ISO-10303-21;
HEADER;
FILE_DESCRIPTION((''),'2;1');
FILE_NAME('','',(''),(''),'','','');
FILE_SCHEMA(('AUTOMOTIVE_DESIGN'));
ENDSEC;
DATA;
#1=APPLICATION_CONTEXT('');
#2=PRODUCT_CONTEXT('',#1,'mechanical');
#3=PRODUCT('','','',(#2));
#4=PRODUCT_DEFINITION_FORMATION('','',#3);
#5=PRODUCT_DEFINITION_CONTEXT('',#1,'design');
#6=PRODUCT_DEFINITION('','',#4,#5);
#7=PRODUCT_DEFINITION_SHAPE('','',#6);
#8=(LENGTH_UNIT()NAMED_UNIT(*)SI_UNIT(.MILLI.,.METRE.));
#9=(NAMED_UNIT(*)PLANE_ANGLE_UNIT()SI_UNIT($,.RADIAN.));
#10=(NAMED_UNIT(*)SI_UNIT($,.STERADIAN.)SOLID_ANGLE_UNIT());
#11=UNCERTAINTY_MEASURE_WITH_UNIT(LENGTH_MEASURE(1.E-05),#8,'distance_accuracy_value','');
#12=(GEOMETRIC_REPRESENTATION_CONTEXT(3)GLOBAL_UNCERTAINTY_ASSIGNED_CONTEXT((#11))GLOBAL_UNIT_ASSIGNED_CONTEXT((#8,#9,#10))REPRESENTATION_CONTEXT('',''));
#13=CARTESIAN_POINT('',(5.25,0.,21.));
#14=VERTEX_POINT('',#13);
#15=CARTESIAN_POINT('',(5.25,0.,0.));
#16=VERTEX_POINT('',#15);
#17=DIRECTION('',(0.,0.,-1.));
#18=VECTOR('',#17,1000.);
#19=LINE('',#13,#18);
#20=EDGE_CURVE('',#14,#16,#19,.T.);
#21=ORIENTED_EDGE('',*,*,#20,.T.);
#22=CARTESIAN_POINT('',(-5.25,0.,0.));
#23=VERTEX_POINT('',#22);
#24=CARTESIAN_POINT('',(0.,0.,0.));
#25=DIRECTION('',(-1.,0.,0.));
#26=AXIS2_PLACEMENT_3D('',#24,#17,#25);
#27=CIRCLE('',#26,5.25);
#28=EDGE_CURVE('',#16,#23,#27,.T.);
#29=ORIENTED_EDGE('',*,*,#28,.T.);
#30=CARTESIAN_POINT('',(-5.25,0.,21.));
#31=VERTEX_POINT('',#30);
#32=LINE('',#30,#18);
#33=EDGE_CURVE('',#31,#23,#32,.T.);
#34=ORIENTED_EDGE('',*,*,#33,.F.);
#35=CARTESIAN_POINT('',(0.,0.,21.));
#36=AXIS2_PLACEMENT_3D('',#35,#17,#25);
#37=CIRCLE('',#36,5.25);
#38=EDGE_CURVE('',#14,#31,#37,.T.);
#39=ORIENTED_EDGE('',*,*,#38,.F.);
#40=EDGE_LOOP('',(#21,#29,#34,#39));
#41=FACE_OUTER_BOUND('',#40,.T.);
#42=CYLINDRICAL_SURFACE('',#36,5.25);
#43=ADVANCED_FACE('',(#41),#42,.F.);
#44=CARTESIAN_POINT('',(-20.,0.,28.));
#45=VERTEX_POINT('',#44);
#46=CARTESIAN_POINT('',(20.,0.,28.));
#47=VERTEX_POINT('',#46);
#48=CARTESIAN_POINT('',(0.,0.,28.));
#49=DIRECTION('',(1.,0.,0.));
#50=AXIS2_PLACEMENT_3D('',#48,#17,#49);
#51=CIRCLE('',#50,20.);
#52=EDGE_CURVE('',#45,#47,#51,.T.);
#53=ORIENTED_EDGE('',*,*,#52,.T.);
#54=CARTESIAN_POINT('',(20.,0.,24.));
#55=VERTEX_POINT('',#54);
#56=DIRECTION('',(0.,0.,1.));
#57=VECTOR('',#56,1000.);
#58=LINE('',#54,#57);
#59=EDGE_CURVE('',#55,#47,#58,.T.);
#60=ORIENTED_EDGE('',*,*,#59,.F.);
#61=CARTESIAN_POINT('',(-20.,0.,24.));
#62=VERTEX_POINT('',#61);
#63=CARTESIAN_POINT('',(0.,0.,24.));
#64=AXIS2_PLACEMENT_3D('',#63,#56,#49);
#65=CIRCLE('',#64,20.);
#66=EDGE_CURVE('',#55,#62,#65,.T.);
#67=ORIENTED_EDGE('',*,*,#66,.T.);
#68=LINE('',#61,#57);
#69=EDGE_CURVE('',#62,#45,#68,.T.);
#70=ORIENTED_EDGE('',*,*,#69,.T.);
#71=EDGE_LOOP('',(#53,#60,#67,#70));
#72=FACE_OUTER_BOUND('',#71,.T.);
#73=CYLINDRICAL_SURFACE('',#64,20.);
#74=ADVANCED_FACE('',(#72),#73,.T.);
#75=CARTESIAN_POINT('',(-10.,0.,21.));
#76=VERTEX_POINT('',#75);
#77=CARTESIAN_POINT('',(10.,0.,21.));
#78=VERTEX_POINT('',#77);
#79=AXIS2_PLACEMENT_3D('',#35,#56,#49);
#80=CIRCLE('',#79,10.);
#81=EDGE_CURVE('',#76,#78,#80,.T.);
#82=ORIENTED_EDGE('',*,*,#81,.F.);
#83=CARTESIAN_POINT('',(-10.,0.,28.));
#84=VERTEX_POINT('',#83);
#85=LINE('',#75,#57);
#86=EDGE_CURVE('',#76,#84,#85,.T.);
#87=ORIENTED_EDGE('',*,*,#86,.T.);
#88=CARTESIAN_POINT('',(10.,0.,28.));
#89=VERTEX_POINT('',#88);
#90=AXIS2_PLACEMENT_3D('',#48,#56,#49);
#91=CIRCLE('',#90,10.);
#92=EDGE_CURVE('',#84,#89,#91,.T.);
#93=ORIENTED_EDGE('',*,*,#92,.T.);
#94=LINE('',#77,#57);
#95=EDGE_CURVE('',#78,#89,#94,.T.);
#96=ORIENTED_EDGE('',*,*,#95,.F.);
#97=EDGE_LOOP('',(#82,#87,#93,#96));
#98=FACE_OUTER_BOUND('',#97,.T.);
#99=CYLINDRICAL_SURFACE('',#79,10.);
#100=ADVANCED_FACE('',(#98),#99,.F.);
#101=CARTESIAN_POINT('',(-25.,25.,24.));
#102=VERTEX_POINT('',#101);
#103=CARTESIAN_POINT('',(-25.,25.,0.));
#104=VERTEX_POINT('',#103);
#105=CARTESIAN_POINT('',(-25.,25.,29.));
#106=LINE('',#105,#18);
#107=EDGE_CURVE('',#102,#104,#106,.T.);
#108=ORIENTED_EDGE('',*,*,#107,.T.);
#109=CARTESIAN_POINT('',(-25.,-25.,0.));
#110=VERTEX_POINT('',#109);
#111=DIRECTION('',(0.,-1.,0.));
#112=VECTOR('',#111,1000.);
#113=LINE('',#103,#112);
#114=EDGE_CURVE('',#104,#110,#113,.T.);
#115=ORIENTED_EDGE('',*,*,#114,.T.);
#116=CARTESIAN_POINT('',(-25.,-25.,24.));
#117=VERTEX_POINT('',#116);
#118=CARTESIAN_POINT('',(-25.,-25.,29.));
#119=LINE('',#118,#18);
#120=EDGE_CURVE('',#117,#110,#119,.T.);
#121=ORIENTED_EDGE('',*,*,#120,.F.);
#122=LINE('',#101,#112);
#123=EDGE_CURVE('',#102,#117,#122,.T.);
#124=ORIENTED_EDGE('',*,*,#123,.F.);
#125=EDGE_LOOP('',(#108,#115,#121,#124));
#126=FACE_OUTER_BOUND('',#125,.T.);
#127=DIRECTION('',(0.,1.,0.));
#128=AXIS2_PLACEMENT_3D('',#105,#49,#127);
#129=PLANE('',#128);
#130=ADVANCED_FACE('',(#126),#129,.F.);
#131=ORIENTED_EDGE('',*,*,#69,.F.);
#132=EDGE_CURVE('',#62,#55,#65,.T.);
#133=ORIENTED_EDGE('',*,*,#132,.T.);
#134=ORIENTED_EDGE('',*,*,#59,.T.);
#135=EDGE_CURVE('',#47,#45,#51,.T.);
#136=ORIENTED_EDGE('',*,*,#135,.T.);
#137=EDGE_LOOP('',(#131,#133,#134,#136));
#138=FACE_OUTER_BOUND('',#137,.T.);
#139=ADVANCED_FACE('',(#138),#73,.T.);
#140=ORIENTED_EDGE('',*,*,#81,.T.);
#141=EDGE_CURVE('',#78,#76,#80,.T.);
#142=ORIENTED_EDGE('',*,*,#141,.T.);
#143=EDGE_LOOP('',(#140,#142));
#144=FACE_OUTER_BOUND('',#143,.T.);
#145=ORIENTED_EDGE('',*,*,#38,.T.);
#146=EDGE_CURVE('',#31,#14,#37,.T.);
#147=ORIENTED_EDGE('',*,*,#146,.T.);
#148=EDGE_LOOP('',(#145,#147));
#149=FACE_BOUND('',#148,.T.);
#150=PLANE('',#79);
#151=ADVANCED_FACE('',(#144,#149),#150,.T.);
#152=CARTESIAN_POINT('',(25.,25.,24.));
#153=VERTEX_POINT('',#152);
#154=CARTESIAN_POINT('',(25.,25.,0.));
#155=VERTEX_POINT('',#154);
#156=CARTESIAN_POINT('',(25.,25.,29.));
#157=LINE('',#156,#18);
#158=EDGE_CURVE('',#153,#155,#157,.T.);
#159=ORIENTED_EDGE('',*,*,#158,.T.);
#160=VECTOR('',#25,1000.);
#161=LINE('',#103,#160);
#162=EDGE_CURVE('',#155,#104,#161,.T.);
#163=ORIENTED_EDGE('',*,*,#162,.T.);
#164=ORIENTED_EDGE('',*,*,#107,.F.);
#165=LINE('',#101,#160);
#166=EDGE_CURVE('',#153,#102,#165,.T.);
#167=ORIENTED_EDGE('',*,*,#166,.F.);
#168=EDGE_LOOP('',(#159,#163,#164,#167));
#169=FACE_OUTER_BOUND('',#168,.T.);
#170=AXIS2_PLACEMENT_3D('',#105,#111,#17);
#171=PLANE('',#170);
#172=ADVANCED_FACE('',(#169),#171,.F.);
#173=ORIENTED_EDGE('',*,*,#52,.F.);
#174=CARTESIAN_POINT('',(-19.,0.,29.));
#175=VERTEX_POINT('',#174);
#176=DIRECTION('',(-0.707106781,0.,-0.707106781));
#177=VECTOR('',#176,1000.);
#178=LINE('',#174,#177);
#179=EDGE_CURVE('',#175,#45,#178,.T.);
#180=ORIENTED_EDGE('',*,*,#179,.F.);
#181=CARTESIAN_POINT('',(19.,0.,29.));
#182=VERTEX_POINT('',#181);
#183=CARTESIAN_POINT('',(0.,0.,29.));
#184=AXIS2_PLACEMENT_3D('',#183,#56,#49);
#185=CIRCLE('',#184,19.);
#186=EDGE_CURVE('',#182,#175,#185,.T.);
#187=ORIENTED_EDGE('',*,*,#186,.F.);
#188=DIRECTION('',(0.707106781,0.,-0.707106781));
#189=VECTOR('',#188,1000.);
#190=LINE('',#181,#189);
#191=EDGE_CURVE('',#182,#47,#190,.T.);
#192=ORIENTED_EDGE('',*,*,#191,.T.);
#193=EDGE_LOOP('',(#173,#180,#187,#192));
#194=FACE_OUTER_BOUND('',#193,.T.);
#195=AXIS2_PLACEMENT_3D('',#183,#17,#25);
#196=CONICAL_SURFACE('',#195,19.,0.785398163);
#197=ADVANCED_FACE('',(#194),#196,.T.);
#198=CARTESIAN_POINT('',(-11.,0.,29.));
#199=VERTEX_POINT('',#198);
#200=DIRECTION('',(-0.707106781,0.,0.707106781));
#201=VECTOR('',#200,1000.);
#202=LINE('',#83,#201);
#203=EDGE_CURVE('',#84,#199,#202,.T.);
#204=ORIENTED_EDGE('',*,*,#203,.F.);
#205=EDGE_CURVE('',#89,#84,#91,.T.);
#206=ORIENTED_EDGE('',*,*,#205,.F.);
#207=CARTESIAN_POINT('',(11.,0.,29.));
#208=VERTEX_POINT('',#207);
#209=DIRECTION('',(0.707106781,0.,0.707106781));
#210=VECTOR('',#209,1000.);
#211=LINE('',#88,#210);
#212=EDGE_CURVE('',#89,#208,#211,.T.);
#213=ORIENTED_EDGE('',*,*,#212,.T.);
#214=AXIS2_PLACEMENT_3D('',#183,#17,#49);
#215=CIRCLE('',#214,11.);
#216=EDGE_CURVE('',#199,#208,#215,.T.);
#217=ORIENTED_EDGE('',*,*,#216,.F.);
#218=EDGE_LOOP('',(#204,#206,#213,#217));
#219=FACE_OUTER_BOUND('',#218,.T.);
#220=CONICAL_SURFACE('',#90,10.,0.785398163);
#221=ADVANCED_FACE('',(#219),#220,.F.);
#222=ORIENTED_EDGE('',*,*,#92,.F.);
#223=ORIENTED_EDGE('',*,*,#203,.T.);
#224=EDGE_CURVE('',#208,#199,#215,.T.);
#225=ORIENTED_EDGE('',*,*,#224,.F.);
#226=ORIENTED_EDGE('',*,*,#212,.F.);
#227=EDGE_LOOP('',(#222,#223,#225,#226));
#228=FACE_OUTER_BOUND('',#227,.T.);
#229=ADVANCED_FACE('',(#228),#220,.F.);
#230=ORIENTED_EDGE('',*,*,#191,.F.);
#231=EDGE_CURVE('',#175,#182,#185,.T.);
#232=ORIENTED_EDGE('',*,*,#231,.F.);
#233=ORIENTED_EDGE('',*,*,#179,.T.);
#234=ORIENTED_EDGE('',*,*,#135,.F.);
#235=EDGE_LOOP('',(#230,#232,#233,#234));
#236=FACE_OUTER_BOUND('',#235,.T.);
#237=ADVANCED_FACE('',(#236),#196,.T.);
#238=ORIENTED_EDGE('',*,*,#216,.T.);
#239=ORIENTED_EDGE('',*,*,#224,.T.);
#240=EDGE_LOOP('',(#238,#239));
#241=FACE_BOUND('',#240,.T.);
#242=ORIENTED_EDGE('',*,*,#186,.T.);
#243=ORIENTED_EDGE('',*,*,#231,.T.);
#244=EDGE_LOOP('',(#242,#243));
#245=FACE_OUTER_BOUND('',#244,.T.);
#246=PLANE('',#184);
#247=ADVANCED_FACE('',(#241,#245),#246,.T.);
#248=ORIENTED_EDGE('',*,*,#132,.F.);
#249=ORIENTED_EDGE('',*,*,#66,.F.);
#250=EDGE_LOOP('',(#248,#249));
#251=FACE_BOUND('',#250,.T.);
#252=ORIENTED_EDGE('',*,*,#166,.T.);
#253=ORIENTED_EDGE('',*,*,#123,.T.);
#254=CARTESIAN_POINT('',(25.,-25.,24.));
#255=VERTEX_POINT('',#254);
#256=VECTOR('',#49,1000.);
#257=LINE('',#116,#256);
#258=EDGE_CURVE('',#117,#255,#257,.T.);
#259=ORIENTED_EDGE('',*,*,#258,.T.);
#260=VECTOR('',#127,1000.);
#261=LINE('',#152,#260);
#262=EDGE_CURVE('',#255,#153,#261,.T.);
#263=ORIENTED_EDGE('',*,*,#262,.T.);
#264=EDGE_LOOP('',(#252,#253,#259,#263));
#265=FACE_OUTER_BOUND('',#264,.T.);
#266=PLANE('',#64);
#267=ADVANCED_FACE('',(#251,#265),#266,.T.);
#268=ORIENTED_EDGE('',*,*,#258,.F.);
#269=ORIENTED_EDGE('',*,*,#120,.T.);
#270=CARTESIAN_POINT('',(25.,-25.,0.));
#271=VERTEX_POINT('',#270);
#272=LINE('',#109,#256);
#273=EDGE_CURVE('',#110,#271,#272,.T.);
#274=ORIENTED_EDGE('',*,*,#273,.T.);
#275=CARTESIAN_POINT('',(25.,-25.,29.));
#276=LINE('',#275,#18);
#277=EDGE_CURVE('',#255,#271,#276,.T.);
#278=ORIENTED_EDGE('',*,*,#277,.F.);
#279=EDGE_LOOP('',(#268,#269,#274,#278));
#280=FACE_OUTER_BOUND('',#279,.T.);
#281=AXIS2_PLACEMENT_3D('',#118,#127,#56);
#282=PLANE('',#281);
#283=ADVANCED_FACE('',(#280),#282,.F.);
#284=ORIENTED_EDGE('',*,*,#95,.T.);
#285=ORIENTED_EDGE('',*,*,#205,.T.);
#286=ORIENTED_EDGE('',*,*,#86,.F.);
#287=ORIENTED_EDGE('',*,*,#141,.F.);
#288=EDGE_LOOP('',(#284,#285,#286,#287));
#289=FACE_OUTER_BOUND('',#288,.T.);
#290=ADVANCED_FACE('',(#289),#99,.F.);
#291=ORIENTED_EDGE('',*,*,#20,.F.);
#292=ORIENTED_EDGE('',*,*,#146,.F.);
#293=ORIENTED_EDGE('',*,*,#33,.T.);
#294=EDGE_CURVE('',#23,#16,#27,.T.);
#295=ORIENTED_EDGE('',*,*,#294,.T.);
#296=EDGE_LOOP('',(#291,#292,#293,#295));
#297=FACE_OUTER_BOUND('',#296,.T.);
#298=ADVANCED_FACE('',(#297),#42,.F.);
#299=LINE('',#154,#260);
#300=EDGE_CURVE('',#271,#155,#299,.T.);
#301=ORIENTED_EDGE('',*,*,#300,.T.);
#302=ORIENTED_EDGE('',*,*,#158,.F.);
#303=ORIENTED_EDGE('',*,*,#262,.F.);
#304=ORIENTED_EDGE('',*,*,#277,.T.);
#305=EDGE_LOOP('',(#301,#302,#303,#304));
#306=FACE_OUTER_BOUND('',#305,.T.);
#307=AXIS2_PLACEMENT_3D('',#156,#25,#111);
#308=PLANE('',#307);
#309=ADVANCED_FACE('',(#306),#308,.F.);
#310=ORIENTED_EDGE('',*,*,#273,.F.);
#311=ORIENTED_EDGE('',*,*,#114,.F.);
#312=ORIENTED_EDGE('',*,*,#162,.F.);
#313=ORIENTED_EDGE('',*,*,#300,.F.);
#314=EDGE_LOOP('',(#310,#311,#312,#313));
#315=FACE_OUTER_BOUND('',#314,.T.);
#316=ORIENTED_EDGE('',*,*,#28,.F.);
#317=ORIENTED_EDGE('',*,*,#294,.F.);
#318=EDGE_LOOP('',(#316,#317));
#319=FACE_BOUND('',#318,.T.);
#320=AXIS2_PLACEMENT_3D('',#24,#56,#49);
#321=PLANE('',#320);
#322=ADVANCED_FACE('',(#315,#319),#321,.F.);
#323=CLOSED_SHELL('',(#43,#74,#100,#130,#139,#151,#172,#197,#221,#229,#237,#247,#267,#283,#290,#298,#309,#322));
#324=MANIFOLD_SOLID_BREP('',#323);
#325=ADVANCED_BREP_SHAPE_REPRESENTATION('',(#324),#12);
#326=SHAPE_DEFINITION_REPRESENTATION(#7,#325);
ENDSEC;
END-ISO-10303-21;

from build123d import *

# Parameters (mm, degrees)
SKETCH_1_W          = 50
SKETCH_1_H          = 50
EXTRUDE_1_DEPTH     = 29
SKETCH_3_R          = 10
CUT_EXTRUDE_1_DEPTH = 8
SKETCH_4_R          = 5.25
CUT_EXTRUDE_2_DEPTH = 21
CHAMFER_1_SIZE      = 1
SKETCH_5_OUTSIDE_W  = 67.286
SKETCH_5_OUTSIDE_H  = 67.286
SKETCH_5_OUTSIDE_R  = 20
CUT_EXTRUDE_3_DEPTH = 5
CHAMFER_2_SIZE      = 1


with BuildPart() as part:
    # 草图1 → 凸台-拉伸1 (new body)
    with BuildSketch(Plane.XY):
        Rectangle(SKETCH_1_W, SKETCH_1_H)
    extrude(amount=EXTRUDE_1_DEPTH)

    # 草图3 → 切除-拉伸1 (cut)
    with BuildSketch(Plane.XY.offset(29)):
        Circle(SKETCH_3_R)
    extrude(amount=-CUT_EXTRUDE_1_DEPTH, mode=Mode.SUBTRACT)

    # 草图4 → 切除-拉伸2 (cut)
    with BuildSketch(Plane(origin=(0, 0, 0), x_dir=(-1, 0, 0), z_dir=(0, 0, -1))):
        Circle(SKETCH_4_R)
    extrude(amount=-CUT_EXTRUDE_2_DEPTH, mode=Mode.SUBTRACT)

    # 倒角1
    chamfer_1_edges = [part.edges().sort_by_distance(p)[0] for p in [
        (-10, 0, 29),
    ]]
    chamfer(chamfer_1_edges, length=CHAMFER_1_SIZE)

    # 草图5 outside → 切除-拉伸3 (cut)
    with BuildSketch(Plane.XY.offset(29)):
        Rectangle(SKETCH_5_OUTSIDE_W, SKETCH_5_OUTSIDE_H)
        Circle(SKETCH_5_OUTSIDE_R, mode=Mode.SUBTRACT)
    extrude(amount=-CUT_EXTRUDE_3_DEPTH, mode=Mode.SUBTRACT)

    # 倒角2
    chamfer_2_edges = [part.edges().sort_by_distance(p)[0] for p in [
        (-20, 0, 29),
    ]]
    chamfer(chamfer_2_edges, length=CHAMFER_2_SIZE)


solid = part.part
